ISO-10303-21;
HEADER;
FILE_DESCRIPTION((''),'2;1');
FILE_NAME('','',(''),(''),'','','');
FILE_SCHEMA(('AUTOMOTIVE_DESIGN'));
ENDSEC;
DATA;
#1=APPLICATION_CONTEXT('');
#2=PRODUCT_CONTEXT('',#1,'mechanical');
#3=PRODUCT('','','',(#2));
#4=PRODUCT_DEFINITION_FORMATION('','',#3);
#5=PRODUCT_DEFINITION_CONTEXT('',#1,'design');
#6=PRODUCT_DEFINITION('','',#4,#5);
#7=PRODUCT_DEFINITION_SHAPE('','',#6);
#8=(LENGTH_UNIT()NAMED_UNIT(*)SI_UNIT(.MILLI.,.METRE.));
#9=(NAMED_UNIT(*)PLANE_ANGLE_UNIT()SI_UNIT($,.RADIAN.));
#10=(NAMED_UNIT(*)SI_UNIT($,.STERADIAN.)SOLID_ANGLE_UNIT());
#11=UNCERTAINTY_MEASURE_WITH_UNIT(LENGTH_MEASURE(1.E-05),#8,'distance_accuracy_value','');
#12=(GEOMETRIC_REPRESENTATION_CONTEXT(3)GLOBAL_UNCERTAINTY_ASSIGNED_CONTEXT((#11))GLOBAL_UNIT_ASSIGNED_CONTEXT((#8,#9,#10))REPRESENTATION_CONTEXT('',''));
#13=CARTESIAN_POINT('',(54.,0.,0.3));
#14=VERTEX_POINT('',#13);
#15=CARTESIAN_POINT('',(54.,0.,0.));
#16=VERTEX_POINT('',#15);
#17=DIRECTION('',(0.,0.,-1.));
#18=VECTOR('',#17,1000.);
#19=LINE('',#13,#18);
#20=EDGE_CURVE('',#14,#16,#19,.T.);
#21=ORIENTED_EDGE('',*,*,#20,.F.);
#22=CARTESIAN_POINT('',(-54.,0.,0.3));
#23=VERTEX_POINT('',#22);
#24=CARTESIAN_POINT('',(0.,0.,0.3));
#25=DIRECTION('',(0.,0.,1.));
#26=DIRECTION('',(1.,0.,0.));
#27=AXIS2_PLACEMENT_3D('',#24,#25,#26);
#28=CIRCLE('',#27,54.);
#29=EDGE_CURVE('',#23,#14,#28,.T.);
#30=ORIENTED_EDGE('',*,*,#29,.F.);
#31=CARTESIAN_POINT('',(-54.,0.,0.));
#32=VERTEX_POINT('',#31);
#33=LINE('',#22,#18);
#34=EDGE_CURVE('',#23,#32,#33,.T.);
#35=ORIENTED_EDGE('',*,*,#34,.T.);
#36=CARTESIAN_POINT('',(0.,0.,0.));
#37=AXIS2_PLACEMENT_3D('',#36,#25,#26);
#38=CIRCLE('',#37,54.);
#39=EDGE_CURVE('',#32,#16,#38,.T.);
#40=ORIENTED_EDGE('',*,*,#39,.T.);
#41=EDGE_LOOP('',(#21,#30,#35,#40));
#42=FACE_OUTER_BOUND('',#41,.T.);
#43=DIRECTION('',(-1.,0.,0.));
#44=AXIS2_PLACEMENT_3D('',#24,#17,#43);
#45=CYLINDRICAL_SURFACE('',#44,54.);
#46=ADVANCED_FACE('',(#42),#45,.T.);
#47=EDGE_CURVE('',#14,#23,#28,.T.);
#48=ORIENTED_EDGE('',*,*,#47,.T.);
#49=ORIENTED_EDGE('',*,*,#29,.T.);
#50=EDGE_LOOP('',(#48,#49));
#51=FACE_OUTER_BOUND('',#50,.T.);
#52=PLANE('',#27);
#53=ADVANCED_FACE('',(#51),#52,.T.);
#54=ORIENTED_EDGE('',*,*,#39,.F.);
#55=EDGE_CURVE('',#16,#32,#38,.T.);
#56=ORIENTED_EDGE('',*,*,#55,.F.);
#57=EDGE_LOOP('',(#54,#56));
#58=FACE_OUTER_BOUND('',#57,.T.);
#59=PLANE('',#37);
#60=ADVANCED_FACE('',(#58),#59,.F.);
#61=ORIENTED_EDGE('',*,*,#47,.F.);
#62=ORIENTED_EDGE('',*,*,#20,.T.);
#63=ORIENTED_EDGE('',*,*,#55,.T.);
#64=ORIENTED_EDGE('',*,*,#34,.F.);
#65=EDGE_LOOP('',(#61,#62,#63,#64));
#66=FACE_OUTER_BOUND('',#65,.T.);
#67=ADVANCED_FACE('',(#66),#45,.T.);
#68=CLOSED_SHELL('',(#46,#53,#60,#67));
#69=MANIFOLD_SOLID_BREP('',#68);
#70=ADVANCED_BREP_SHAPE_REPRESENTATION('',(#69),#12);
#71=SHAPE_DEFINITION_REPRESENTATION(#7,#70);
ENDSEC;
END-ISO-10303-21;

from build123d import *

# Parameters (mm, degrees)
SKETCH_1_R      = 54
EXTRUDE_1_DEPTH = 0.3


with BuildPart() as part:
    # 草图1 → 凸台-拉伸1 (new body)
    with BuildSketch(Plane.XY):
        Circle(SKETCH_1_R)
    extrude(amount=EXTRUDE_1_DEPTH)


solid = part.part
